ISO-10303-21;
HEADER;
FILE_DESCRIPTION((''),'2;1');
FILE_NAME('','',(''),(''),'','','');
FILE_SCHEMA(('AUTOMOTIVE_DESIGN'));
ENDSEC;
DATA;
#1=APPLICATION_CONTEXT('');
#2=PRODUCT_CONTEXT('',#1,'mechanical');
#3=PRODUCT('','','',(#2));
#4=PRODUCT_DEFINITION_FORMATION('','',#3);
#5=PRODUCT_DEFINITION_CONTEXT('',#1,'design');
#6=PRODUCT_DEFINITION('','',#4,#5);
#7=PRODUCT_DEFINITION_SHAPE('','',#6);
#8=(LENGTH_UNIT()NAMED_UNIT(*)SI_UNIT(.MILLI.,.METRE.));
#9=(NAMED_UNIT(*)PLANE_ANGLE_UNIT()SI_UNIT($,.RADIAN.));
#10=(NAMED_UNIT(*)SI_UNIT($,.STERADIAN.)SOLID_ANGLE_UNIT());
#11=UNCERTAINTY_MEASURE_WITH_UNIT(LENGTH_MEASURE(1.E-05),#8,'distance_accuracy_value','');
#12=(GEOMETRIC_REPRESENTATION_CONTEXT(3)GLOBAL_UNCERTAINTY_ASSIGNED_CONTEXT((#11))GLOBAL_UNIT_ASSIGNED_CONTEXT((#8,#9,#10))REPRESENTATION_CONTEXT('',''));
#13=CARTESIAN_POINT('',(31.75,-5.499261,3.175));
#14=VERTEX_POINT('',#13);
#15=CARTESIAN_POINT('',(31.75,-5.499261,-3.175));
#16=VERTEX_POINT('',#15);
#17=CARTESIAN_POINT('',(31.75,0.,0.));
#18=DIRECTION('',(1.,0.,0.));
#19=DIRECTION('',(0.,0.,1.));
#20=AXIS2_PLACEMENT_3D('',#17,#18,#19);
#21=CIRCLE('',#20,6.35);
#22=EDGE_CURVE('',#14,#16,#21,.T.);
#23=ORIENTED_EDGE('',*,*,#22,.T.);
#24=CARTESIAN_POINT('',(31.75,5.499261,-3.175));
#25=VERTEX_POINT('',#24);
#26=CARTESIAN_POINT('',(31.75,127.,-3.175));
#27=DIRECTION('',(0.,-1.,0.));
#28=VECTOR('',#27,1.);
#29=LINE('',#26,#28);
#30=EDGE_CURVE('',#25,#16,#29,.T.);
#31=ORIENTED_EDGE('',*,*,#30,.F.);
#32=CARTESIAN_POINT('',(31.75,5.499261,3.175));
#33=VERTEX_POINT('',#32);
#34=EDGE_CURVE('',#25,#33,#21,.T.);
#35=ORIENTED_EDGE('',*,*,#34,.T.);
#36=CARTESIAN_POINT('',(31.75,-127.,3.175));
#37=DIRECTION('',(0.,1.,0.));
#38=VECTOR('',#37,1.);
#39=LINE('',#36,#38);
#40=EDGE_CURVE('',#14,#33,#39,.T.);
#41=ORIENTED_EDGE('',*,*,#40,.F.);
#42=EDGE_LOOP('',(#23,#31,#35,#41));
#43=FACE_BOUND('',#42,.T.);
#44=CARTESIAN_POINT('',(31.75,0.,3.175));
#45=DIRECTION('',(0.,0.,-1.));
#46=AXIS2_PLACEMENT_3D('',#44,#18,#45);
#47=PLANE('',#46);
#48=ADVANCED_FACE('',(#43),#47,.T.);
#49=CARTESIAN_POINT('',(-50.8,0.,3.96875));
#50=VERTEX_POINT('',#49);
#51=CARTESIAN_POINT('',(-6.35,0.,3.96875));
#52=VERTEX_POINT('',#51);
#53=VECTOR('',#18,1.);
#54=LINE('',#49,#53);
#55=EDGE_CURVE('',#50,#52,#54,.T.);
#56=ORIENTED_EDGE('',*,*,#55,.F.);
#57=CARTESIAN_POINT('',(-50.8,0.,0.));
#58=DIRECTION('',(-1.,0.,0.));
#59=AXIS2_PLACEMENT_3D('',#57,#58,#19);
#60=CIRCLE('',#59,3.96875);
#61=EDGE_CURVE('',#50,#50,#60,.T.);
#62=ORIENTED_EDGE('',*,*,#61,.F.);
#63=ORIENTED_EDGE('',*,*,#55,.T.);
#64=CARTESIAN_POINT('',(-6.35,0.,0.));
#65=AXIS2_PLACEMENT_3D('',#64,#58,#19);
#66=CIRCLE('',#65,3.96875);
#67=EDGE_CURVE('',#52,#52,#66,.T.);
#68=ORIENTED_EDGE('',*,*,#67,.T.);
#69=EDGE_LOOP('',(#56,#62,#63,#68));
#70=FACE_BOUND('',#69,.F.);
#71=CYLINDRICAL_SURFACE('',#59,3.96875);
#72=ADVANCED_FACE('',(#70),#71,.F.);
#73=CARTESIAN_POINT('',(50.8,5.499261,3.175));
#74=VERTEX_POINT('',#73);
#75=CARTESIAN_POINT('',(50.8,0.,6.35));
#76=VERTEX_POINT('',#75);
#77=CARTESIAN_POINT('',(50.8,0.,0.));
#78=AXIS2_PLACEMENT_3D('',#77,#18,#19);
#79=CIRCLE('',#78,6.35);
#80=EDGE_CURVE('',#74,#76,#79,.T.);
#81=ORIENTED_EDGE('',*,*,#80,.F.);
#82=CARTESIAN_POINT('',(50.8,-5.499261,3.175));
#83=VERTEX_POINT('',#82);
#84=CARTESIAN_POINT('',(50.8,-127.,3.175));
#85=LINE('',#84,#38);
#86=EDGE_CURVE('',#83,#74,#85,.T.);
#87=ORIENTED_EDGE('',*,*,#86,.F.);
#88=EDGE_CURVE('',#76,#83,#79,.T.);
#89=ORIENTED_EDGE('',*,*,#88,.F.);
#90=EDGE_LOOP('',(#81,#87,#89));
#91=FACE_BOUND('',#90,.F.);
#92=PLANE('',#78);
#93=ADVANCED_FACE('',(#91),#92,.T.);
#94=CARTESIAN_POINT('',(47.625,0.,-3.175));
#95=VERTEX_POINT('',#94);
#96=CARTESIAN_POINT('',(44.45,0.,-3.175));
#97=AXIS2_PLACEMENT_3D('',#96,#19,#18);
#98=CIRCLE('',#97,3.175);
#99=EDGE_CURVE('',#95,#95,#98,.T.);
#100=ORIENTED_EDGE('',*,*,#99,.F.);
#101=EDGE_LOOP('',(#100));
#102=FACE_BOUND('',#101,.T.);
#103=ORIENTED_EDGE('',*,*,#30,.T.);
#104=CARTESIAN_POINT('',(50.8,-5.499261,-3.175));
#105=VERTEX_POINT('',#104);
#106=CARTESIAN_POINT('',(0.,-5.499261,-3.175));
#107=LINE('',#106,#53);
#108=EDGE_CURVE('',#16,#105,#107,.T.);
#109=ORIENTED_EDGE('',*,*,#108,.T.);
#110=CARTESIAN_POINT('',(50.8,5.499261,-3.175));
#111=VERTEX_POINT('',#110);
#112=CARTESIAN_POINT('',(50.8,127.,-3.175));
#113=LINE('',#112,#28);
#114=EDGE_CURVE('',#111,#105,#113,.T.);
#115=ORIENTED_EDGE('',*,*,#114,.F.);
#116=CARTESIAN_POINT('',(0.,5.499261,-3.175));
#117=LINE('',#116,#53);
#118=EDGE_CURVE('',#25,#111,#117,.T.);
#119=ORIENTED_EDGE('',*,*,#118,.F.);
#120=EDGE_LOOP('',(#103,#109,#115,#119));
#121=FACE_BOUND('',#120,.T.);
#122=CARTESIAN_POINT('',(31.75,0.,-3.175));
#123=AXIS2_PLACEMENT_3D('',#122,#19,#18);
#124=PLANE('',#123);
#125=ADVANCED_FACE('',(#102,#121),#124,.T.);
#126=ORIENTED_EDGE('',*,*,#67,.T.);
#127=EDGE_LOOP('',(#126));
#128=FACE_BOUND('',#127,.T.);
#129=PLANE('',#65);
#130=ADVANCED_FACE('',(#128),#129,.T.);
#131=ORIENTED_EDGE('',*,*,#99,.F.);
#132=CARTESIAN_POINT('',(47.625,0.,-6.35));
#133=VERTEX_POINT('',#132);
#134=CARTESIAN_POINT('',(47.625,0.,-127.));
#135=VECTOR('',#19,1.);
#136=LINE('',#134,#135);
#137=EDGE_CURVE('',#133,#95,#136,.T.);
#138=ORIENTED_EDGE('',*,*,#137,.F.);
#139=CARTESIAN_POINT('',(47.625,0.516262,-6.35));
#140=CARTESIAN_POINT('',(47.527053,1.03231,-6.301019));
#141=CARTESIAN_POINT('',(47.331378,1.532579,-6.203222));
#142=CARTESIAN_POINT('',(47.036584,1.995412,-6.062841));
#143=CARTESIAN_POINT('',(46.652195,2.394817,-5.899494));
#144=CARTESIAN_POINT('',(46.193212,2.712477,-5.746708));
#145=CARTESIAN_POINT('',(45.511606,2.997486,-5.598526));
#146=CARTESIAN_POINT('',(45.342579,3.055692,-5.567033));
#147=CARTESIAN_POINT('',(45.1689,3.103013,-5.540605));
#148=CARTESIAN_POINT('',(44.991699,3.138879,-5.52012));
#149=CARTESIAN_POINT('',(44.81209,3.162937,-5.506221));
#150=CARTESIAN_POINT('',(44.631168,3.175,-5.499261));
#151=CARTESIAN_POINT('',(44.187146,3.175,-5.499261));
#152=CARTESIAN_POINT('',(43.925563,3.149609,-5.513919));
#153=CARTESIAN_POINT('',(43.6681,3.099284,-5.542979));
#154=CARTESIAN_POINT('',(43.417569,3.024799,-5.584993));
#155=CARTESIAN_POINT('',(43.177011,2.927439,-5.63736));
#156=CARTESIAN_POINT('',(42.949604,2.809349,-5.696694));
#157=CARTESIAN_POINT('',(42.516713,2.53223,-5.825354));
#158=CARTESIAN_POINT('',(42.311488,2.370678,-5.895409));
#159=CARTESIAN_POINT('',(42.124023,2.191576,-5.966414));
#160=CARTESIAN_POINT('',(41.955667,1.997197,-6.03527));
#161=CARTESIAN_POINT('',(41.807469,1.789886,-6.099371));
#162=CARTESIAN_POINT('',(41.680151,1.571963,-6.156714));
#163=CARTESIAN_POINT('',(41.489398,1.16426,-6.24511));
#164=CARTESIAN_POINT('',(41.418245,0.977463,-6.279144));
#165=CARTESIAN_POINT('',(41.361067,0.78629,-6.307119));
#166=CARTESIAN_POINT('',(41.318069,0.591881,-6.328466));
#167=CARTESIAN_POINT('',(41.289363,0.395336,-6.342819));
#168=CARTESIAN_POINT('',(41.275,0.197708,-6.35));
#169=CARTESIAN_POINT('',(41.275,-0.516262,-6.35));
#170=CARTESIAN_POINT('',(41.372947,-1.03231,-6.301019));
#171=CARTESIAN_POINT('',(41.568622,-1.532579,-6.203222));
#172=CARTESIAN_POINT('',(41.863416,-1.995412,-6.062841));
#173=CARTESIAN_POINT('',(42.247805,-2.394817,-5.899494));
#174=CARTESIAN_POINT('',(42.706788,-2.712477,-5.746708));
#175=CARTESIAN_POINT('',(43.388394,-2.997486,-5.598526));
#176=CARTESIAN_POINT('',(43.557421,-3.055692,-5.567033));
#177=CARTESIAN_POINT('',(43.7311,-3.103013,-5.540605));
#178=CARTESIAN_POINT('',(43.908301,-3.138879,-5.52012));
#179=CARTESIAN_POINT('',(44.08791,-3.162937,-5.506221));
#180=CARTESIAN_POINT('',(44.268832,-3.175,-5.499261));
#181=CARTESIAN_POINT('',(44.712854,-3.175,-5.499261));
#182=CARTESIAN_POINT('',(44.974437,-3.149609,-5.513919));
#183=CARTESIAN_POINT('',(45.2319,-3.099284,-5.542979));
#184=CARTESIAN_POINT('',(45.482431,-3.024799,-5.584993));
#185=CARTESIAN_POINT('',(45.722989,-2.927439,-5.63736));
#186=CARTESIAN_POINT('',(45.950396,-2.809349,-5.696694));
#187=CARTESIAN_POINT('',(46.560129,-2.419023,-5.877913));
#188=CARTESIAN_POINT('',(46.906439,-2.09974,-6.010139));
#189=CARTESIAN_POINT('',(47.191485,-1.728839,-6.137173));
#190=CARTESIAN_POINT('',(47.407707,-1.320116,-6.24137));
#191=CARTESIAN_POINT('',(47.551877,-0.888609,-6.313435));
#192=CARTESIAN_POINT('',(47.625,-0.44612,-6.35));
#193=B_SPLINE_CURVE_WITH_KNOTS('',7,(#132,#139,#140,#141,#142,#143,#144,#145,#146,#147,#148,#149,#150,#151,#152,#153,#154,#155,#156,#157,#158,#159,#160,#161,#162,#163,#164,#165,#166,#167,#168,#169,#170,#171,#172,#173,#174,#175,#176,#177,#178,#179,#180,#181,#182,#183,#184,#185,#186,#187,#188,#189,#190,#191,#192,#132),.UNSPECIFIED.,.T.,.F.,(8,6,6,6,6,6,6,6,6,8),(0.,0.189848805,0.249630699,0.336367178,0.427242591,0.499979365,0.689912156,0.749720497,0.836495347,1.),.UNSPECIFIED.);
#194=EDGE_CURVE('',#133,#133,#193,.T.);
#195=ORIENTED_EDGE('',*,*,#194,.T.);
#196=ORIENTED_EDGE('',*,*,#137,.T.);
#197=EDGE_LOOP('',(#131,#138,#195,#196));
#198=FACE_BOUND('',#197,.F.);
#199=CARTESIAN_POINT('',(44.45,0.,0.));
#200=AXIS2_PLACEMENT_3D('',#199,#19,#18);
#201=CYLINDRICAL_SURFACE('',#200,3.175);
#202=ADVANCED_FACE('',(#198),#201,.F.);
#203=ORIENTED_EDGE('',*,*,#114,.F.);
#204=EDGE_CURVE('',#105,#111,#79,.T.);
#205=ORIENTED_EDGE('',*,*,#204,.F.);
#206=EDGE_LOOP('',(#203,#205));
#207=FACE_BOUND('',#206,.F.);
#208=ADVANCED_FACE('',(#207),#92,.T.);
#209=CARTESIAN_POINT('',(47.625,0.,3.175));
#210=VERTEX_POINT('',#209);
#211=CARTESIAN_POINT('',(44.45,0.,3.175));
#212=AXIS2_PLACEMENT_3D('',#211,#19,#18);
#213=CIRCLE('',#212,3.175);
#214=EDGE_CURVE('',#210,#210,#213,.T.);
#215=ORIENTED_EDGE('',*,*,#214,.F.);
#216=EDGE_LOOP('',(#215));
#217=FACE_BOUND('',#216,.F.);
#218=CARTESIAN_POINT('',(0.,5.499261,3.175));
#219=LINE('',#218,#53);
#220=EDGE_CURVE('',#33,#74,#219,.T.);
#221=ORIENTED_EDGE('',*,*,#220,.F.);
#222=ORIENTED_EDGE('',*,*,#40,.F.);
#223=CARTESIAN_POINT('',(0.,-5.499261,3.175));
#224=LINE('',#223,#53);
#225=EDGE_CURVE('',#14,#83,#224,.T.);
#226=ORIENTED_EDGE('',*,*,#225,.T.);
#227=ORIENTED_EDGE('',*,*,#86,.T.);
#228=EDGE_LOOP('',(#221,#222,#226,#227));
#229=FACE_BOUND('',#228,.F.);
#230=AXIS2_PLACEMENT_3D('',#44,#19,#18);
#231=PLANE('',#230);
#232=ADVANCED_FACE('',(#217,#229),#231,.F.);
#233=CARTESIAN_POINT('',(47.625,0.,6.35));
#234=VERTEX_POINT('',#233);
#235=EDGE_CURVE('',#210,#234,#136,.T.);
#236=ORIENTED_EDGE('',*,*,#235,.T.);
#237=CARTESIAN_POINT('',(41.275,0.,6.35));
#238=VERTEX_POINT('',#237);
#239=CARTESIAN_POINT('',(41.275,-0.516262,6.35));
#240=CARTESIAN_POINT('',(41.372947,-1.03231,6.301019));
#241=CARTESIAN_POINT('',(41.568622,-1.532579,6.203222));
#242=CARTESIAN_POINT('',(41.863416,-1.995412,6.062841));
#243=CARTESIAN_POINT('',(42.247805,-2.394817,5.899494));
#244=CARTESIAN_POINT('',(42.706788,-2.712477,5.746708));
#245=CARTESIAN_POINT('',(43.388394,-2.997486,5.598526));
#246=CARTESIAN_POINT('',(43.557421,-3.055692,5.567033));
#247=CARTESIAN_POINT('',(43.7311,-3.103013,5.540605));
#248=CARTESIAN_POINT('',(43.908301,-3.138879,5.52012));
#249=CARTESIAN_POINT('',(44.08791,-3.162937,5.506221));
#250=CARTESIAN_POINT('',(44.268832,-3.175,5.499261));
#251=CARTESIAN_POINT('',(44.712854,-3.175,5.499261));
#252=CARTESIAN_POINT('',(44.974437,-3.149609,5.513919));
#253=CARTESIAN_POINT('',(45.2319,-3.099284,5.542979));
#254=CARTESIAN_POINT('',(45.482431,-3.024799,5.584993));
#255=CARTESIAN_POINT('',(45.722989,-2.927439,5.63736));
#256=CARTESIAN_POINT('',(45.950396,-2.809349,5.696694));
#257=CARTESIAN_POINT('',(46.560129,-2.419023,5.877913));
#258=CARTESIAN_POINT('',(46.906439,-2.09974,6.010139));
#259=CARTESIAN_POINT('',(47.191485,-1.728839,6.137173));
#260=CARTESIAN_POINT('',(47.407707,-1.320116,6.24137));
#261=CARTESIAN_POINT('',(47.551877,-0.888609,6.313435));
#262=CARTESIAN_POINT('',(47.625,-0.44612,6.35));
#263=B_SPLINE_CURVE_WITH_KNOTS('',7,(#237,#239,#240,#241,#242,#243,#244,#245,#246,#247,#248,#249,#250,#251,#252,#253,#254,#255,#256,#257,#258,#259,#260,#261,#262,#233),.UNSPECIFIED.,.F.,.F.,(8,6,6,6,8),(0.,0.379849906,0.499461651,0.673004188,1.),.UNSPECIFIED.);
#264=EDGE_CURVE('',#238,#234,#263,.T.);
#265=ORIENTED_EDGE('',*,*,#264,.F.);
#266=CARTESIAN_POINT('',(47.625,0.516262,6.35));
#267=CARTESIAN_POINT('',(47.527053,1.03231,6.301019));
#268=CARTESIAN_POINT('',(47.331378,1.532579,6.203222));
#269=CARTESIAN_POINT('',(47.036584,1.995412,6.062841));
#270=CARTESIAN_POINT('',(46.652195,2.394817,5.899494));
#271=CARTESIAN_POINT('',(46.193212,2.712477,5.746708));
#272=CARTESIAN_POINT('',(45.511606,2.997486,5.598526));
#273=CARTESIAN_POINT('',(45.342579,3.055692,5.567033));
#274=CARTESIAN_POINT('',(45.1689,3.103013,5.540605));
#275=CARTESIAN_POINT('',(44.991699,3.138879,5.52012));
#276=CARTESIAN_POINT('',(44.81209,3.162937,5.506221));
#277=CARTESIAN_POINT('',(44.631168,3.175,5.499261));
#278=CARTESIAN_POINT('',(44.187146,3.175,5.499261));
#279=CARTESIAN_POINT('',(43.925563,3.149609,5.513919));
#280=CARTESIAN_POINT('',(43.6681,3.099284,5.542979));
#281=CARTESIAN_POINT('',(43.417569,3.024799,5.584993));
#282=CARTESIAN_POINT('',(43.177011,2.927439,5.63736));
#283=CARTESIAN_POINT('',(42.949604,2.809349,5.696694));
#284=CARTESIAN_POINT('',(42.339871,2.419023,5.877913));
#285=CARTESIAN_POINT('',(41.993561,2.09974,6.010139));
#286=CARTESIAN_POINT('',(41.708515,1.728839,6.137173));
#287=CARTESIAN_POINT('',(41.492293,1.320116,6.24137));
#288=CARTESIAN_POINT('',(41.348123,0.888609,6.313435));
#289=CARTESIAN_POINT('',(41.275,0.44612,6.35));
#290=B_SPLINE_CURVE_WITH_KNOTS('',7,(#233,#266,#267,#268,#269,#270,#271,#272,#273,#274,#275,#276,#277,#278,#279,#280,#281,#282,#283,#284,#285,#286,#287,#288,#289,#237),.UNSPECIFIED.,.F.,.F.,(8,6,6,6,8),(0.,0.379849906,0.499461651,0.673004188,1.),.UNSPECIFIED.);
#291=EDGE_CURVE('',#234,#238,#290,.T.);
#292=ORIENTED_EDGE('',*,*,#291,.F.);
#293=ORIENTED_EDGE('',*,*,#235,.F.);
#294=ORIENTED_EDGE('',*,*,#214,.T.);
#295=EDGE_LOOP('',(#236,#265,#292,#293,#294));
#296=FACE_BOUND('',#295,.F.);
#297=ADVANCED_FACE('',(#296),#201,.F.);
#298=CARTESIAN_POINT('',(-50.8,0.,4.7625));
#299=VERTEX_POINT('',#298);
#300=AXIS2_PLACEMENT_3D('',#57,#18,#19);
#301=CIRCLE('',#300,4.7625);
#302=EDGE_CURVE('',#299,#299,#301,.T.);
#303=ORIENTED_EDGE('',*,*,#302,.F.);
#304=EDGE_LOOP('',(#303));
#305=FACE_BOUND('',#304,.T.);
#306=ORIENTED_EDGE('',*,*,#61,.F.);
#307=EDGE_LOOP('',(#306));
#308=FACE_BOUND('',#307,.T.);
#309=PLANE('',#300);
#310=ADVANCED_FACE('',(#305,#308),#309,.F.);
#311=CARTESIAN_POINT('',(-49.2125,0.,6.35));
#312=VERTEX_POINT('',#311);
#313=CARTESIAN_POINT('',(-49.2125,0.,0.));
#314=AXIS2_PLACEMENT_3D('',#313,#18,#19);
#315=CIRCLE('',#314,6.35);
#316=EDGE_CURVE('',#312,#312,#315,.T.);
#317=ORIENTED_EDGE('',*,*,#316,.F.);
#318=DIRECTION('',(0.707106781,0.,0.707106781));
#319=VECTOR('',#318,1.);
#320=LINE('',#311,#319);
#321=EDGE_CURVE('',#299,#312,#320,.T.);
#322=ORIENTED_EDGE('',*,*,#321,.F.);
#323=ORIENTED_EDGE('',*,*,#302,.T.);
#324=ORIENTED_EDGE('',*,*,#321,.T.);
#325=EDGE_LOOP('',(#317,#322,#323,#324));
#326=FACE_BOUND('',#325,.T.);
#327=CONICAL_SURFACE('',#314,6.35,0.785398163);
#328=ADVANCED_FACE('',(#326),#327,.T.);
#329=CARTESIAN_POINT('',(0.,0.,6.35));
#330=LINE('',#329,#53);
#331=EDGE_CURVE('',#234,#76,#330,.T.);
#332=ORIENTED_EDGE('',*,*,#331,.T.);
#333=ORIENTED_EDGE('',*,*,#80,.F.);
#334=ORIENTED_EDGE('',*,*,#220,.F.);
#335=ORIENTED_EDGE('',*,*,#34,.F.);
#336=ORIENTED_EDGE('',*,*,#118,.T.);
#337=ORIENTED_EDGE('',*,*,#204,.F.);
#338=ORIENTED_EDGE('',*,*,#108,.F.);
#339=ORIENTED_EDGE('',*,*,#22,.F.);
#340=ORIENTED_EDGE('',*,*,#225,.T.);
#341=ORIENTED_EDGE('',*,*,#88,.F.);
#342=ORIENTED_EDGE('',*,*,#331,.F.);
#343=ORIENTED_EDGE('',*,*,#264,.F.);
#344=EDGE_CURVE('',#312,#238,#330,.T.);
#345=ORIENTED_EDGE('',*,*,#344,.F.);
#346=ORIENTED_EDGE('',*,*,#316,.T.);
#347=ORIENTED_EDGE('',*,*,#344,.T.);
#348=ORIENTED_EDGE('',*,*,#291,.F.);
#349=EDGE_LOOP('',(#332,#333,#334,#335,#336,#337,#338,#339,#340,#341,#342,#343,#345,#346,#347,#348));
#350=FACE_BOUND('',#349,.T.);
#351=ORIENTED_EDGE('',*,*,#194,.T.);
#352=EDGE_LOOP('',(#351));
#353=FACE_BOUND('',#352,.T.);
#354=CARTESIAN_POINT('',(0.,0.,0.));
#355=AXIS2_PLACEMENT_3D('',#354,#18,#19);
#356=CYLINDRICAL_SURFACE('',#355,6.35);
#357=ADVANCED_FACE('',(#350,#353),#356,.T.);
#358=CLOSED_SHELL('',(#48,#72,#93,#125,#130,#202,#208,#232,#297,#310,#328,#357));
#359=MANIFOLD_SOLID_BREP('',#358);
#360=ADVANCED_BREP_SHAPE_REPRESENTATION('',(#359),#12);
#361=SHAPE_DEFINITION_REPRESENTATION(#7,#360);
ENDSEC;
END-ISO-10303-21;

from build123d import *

# Parameters (mm, degrees)
ROD_PROFILE_SKETCH_W      = 4
ROD_PROFILE_SKETCH_H      = 0.25
END_NOTCH_SKETCH_R        = 0.125
END_NOTCH_CUT_DEPTH       = 5
CLEVIS_SLOT_SKETCH_W      = 0.75
CLEVIS_SLOT_SKETCH_H      = 0.25
CLEVIS_SLOT_DEPTH         = 5
CROSS_PIN_HOLE_SKETCH_R   = 0.15625
CROSS_PIN_HOLE_DEPTH      = 1.75
END_CHAMFER_SIZE          = 0.0625
SCALE_TO_FINAL_SIZE_SCALE = 25.4


with BuildPart() as part:
    # Rod Profile Sketch → Rod Body (revolve)
    with BuildSketch(Plane.XY, mode=Mode.PRIVATE) as rod_body_sk:
        with Locations((0, 0.125)):
            Rectangle(ROD_PROFILE_SKETCH_W, ROD_PROFILE_SKETCH_H)
    revolve(rod_body_sk.sketch.rotate(Axis((-2.293403827, 0, 0), (1, 0, 0)), 90), axis=Axis((-2.293403827, 0, 0), (1, 0, 0)))

    # End Notch Sketch → End Notch Cut (cut, symmetric)
    with BuildSketch(Plane.XY):
        with Locations((1.75, 0)):
            Circle(END_NOTCH_SKETCH_R)
    extrude(amount=END_NOTCH_CUT_DEPTH, both=True, mode=Mode.SUBTRACT)

    # Clevis Slot Sketch → Clevis Slot (cut, symmetric)
    with BuildSketch(Plane(origin=(0, 0, 0), x_dir=(1, 0, 0), z_dir=(0, 1, 0))):
        with Locations((1.625, 0)):
            Rectangle(CLEVIS_SLOT_SKETCH_W, CLEVIS_SLOT_SKETCH_H)
    extrude(amount=CLEVIS_SLOT_DEPTH, both=True, mode=Mode.SUBTRACT)

    # Cross Pin Hole Sketch → Cross Pin Hole (cut)
    with BuildSketch(Plane.ZY.offset(2)):
        Circle(CROSS_PIN_HOLE_SKETCH_R)
    extrude(amount=-CROSS_PIN_HOLE_DEPTH, mode=Mode.SUBTRACT)

    # End Chamfer
    end_chamfer_edges = [part.edges().sort_by_distance(p)[0] for p in [
        (-2, 0, -0.25),
    ]]
    chamfer(end_chamfer_edges, length=END_CHAMFER_SIZE)


with BuildPart() as part_1:
    # Scale to Final Size: scaled about (0, 0, 0)
    add(part.part.scale(SCALE_TO_FINAL_SIZE_SCALE))


solid = part_1.part
